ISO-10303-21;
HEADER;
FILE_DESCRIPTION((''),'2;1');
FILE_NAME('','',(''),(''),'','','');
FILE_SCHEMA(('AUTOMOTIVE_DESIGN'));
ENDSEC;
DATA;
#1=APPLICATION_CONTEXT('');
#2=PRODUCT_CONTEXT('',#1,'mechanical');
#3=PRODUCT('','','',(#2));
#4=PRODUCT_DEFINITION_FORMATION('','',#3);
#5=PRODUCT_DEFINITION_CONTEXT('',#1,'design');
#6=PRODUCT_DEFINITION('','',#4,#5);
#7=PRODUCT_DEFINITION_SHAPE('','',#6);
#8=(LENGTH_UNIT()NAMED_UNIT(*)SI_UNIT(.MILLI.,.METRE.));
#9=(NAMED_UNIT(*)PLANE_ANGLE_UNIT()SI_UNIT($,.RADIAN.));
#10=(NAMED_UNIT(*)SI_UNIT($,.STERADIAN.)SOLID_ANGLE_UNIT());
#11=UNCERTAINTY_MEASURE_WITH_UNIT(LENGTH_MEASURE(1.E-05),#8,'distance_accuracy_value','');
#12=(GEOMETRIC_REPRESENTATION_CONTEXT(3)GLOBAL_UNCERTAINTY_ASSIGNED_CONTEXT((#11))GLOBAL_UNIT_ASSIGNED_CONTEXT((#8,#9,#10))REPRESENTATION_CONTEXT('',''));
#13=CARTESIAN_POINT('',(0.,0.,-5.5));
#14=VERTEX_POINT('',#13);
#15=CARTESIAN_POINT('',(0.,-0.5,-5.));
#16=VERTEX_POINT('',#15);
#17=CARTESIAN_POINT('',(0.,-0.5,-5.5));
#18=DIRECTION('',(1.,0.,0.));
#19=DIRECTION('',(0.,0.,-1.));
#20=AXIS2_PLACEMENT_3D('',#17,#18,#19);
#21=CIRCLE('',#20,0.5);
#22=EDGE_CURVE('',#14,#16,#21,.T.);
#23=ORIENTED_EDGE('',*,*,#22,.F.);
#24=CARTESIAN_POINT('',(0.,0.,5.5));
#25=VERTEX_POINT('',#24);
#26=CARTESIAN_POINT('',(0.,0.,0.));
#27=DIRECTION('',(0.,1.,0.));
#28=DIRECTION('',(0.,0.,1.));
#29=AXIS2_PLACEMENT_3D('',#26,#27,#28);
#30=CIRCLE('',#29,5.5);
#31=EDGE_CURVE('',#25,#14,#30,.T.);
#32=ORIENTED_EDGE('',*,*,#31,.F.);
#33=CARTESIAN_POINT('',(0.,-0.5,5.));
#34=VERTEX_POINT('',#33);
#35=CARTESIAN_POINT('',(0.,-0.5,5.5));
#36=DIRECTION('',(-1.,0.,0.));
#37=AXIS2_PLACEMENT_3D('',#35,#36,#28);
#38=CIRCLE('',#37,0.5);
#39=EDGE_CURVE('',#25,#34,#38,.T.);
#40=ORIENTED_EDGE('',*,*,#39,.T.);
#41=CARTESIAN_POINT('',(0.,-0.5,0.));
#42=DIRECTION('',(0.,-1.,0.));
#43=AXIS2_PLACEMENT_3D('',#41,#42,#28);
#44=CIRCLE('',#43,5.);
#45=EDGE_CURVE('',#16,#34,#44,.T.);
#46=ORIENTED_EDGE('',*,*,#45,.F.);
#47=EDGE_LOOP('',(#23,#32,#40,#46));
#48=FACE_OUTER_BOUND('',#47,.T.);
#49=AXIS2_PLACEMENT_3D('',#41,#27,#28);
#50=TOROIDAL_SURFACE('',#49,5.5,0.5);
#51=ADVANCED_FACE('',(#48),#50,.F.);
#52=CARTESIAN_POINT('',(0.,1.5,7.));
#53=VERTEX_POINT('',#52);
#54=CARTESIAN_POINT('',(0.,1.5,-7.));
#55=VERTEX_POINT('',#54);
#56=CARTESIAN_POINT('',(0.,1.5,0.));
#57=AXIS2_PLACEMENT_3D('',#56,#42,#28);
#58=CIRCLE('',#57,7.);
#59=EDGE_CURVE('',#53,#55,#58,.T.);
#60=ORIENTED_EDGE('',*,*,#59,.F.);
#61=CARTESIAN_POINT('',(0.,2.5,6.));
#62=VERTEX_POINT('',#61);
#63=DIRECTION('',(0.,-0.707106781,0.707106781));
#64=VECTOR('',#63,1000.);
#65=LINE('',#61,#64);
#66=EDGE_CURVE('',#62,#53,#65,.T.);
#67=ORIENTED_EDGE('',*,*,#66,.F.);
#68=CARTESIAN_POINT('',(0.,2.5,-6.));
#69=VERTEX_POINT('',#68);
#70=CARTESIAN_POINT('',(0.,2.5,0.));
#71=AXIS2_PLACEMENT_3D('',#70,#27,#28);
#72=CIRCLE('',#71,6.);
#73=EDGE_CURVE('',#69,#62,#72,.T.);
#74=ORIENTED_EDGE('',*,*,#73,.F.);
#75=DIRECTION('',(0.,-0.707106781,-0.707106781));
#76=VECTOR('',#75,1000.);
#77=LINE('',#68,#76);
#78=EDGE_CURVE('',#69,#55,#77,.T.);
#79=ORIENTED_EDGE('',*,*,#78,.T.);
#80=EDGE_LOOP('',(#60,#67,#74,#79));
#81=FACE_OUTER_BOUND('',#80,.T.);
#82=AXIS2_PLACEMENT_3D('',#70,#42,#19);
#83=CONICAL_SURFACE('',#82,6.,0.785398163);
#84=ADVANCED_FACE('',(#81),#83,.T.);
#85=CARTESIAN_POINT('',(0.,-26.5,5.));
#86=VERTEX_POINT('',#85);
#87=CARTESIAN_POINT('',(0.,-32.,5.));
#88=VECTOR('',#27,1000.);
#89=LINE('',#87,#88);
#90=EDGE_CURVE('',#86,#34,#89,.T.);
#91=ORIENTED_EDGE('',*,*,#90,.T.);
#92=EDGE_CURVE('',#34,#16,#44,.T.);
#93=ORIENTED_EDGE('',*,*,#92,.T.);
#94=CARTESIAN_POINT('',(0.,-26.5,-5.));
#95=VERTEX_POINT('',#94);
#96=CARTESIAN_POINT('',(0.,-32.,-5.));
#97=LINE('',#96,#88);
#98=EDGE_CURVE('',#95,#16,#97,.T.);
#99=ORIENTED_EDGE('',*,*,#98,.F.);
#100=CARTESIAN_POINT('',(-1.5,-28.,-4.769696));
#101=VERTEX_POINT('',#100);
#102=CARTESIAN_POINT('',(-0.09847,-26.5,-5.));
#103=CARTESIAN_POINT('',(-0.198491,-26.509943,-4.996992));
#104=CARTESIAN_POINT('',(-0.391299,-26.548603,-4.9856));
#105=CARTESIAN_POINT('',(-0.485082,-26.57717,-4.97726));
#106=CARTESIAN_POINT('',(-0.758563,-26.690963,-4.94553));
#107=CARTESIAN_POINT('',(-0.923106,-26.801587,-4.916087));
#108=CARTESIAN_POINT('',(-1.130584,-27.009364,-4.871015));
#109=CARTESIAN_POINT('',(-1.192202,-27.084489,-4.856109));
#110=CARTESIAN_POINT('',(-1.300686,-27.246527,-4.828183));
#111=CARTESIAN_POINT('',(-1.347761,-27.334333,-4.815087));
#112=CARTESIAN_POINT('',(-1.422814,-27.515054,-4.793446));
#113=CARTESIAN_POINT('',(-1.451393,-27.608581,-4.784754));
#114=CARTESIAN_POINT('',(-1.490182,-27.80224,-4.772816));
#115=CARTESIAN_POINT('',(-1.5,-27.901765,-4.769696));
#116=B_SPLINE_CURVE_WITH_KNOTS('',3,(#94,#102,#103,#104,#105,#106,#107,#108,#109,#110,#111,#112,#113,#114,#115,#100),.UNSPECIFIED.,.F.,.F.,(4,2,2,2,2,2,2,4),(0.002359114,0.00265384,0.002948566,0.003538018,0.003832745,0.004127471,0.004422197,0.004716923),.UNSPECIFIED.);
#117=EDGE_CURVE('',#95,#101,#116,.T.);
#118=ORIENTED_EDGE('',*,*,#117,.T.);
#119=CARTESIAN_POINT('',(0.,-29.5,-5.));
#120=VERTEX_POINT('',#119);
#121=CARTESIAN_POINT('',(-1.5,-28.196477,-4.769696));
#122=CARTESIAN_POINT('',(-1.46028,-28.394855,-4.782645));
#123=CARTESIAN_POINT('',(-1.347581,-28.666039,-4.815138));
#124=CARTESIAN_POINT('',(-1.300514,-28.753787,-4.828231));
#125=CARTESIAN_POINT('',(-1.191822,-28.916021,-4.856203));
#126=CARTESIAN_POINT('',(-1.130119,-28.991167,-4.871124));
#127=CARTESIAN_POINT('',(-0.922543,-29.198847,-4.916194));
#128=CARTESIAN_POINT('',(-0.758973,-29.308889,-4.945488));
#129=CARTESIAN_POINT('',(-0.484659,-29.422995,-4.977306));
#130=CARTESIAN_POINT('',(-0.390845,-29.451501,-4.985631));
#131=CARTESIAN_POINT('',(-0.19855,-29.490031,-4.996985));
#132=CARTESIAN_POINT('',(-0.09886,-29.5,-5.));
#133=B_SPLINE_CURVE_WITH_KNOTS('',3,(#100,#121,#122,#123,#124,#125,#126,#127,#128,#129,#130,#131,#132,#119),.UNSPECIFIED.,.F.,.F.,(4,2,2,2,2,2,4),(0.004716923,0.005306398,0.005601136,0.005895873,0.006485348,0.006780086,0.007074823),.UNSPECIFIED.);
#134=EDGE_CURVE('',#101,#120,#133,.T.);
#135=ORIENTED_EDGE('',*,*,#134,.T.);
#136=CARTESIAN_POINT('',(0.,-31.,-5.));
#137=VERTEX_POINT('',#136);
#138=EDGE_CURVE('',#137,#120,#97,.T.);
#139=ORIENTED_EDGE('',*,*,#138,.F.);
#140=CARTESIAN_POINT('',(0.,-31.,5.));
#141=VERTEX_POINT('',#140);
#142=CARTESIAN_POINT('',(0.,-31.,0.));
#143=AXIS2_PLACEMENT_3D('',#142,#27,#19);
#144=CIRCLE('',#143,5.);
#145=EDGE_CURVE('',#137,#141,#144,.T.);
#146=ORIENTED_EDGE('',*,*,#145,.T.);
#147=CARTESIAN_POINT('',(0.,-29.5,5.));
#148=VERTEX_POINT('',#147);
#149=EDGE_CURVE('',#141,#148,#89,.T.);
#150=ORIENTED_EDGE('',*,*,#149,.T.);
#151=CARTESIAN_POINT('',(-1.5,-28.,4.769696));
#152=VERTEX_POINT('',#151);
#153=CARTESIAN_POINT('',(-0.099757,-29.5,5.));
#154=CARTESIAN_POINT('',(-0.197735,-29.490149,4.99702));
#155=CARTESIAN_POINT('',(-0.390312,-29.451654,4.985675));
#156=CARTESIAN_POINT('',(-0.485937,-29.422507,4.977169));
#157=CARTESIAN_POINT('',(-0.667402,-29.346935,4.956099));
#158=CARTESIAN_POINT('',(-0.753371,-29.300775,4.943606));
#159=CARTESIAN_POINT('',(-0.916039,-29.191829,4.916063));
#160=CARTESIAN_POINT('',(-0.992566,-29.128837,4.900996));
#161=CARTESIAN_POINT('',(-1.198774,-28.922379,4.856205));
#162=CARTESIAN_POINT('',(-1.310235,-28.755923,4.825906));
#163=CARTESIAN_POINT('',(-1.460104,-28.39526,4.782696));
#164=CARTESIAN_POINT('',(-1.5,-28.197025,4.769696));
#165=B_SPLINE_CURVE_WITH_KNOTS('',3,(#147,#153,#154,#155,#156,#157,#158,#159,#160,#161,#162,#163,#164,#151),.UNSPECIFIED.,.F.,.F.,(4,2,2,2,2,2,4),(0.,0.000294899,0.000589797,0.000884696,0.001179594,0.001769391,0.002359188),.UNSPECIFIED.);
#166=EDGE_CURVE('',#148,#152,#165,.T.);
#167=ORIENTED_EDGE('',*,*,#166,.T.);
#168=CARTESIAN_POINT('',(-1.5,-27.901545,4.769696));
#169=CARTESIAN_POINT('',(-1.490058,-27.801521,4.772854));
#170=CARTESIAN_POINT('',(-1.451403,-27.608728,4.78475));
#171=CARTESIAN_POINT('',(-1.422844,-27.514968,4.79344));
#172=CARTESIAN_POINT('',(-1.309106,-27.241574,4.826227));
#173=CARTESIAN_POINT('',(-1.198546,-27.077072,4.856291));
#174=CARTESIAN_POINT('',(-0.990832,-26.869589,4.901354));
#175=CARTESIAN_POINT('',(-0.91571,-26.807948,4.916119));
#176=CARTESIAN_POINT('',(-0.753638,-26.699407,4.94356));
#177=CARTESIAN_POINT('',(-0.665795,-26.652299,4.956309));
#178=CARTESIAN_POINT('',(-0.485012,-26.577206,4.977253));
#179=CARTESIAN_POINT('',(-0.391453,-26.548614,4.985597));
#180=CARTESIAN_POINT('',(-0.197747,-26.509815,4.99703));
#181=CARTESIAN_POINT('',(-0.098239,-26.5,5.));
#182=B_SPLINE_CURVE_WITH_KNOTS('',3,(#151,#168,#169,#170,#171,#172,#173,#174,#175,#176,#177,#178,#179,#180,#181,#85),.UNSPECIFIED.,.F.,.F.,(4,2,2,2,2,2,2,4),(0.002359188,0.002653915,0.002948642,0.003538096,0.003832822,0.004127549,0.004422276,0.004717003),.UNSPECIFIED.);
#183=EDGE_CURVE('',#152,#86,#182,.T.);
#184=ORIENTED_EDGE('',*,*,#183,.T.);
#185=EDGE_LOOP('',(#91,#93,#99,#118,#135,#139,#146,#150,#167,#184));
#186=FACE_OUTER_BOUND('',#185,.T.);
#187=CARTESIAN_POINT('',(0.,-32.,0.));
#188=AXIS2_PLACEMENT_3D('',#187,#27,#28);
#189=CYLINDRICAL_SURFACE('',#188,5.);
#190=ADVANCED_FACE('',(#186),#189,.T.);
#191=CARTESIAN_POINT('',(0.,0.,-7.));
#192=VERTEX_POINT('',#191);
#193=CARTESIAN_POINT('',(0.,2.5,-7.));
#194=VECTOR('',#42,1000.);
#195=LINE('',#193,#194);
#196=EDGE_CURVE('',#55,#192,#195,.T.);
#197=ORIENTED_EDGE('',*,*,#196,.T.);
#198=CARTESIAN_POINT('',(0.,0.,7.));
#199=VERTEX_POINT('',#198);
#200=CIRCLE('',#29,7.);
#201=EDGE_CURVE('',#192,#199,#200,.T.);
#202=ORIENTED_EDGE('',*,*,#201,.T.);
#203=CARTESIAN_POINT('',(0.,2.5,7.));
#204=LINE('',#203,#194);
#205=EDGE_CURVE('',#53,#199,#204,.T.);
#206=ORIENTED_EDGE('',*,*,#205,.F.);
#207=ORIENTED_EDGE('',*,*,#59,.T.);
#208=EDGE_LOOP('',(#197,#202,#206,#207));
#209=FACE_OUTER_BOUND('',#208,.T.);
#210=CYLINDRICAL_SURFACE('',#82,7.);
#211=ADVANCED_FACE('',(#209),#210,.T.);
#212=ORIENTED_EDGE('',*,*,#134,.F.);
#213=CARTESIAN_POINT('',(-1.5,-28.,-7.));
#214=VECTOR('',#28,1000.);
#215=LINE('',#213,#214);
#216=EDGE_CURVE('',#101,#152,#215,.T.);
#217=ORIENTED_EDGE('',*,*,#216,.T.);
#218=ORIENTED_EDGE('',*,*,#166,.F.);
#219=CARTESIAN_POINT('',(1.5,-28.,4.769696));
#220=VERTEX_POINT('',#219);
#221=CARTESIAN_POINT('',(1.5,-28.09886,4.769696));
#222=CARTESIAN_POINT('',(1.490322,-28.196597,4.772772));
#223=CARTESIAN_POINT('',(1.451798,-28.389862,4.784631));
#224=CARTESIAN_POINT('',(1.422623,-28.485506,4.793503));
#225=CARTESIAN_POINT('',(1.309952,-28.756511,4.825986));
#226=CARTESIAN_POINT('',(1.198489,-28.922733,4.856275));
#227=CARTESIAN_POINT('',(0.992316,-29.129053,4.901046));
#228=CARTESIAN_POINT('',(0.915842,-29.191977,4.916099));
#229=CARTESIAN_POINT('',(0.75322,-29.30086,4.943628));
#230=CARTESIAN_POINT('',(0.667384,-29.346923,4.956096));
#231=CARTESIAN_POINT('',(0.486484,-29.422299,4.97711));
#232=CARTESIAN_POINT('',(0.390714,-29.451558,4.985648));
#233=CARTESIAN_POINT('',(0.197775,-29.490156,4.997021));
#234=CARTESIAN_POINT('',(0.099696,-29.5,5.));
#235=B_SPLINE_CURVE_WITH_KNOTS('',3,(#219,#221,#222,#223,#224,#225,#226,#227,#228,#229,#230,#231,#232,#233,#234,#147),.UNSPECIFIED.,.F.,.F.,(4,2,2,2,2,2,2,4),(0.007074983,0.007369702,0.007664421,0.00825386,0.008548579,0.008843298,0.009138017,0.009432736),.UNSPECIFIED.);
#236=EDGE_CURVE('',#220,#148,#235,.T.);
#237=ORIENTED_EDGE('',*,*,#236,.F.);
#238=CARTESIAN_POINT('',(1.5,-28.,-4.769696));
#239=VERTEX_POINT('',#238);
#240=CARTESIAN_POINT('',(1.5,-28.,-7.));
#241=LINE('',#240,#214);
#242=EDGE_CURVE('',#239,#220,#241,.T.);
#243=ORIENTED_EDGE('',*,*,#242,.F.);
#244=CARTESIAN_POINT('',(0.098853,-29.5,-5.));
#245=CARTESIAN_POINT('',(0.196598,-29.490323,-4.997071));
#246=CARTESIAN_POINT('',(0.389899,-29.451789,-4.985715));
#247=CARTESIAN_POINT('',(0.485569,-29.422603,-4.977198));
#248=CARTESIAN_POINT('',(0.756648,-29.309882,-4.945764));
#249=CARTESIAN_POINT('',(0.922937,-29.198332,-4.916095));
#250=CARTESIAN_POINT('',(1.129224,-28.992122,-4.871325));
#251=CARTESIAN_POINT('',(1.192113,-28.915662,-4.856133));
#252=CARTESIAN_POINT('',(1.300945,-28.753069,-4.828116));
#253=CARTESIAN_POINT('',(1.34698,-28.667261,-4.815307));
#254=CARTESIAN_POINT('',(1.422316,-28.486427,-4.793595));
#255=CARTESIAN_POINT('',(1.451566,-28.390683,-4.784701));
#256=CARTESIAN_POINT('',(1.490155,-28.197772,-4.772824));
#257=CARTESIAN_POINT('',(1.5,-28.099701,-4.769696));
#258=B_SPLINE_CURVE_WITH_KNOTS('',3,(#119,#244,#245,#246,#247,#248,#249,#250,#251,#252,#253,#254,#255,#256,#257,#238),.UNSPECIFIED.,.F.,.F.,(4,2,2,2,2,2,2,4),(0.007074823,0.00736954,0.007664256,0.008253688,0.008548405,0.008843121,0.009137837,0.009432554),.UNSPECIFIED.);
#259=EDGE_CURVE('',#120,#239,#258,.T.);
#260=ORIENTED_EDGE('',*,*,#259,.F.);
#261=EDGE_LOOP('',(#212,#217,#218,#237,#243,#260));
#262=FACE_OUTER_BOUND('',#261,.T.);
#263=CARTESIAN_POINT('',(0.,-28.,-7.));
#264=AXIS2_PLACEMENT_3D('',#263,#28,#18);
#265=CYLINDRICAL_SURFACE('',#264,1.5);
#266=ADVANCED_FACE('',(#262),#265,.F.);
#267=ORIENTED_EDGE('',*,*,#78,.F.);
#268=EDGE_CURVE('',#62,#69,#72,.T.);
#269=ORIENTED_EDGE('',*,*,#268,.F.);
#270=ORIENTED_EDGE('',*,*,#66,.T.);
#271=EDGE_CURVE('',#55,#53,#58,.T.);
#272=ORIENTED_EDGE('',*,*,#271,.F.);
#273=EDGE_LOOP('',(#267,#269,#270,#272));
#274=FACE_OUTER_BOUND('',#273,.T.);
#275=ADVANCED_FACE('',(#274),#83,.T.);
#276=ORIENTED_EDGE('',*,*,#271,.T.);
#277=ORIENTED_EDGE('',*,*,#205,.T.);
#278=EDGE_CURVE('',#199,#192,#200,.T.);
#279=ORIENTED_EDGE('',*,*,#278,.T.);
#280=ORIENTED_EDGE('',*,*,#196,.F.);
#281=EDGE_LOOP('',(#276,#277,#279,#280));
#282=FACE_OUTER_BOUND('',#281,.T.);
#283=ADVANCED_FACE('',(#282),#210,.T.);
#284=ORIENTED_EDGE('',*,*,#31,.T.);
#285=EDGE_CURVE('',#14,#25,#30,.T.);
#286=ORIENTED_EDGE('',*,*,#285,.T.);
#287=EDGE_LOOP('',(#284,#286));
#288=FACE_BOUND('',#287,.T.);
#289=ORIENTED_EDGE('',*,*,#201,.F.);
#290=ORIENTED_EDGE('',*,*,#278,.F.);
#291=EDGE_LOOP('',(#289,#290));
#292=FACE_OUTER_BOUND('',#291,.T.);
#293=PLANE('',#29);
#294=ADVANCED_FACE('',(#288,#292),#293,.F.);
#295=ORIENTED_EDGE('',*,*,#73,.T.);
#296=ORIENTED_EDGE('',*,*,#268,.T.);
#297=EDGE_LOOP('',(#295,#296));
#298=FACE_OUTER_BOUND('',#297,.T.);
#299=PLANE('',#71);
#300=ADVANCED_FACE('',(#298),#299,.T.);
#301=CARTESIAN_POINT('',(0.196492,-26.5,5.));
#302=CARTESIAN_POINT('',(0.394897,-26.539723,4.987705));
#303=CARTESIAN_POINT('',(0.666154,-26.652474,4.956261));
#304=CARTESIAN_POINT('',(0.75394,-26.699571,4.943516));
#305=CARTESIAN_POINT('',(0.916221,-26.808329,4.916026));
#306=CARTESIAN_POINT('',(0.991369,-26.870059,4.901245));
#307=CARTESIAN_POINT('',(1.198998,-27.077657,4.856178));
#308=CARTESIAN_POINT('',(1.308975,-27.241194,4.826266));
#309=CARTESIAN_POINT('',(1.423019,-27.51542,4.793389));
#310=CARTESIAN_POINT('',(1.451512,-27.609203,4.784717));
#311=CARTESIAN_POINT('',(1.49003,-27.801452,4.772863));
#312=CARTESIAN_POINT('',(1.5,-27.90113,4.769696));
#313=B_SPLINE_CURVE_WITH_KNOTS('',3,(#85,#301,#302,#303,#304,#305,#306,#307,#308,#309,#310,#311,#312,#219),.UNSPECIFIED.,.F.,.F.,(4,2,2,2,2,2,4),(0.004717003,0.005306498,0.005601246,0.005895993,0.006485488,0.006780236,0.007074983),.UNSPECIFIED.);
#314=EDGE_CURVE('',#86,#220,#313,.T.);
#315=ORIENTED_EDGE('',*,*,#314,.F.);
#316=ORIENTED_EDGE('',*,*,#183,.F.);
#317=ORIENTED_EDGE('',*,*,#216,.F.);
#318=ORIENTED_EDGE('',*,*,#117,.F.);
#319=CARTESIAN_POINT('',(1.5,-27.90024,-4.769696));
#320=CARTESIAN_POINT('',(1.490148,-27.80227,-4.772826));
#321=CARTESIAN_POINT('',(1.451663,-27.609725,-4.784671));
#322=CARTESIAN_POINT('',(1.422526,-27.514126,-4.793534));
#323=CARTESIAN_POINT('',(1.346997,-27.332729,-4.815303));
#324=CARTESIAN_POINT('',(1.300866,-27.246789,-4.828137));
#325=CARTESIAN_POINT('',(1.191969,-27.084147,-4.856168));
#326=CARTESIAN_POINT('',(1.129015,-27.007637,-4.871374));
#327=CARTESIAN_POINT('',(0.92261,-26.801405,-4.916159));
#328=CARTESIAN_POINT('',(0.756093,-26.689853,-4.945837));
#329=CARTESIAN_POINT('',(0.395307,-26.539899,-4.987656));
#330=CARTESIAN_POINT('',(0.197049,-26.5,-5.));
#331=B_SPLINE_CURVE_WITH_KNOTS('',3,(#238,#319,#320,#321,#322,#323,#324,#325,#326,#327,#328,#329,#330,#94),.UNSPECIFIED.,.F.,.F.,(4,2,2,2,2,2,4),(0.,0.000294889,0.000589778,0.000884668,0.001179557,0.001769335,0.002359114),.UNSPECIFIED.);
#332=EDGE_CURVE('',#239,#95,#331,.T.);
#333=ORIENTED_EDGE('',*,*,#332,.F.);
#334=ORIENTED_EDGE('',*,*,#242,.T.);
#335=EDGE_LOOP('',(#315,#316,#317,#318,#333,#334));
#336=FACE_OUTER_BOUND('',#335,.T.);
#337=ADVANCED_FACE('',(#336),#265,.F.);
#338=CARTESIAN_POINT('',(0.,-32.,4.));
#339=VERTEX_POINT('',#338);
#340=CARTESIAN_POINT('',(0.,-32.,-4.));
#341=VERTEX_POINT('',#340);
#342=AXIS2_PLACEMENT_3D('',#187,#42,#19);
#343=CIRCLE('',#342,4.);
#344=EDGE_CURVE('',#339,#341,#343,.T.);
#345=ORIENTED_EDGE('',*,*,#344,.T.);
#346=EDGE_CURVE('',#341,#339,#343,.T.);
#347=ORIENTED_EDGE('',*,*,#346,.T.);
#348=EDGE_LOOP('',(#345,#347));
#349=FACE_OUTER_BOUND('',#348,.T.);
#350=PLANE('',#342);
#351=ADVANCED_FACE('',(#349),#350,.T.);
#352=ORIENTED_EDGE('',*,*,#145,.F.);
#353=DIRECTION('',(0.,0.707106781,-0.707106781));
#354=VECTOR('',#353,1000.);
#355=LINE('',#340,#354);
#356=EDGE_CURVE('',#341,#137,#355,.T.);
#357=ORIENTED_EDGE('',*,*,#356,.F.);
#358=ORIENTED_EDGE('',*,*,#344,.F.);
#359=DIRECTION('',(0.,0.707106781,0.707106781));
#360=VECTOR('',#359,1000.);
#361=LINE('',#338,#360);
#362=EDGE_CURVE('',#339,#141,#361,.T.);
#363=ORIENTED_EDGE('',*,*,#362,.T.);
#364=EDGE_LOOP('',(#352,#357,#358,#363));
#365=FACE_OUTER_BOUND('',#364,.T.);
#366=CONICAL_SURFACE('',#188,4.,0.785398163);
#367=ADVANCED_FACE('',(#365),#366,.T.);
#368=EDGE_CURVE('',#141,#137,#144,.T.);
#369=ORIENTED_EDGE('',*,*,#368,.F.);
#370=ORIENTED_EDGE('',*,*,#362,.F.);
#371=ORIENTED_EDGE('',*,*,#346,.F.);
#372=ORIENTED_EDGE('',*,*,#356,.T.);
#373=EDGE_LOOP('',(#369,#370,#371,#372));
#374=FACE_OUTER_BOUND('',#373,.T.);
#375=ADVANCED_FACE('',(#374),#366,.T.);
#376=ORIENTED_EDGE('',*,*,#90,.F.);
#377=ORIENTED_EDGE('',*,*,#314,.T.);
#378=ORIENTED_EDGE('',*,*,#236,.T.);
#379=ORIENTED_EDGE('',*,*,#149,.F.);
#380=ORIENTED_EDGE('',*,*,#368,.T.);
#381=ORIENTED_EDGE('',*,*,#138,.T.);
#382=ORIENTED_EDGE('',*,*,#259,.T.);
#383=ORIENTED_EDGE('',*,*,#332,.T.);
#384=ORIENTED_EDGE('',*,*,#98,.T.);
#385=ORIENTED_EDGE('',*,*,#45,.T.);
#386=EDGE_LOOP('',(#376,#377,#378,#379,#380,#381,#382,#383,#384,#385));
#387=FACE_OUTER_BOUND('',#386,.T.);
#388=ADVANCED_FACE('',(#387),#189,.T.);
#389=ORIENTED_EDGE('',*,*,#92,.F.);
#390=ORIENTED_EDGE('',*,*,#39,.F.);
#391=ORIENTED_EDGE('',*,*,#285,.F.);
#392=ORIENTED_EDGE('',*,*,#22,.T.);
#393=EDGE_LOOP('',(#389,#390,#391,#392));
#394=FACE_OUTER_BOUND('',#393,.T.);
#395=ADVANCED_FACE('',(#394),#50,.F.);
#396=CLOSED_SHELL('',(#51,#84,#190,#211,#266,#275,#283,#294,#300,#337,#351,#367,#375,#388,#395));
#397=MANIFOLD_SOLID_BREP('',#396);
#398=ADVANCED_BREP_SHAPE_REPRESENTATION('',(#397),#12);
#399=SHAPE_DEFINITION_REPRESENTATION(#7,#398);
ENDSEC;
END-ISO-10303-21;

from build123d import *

# Parameters (mm, degrees)
SKETCH_1_R               = 7
EXTRUDE_1_DEPTH          = 2.5
SKETCH_2_R               = 5
EXTRUDE_2_DEPTH          = 32
CHAMFER_1_SIZE           = 1
CUT_EXTRUDE_2_DEPTH      = 34.496268449
CUT_EXTRUDE_2_DEPTH_BACK = 34.496268449
SKETCH_10_R              = 1.5
FILLET_1_R               = 0.5


with BuildPart() as part:
    # 草图1 → 凸台-拉伸1 (new body)
    with BuildSketch(Plane(origin=(0, 0, 0), x_dir=(1, 0, 0), z_dir=(0, 1, 0))):
        with Locations(Location((0, 0, 0), (0, 0, 270))):
            Circle(SKETCH_1_R)
    extrude(amount=EXTRUDE_1_DEPTH)

    # 草图2 → 凸台-拉伸2 (add)
    with BuildSketch(Plane.XZ):
        with Locations(Location((0, 0, 0), (0, 0, 270))):
            Circle(SKETCH_2_R)
    extrude(amount=EXTRUDE_2_DEPTH)

    # 倒角1
    chamfer_1_edges = [part.edges().sort_by_distance(p)[0] for p in [
        (0, 2.5, -7),
        (0, -32, 5),
    ]]
    chamfer(chamfer_1_edges, length=CHAMFER_1_SIZE)

    # 草图10 → 切除-拉伸2 (cut, two sides: drawn at the far end of the back side and taken through both)
    with BuildSketch(Plane.XY.offset(-CUT_EXTRUDE_2_DEPTH_BACK)):
        with Locations(Location((0, -28, 0), (0, 0, 270.000000018))):
            Circle(SKETCH_10_R)
    extrude(amount=CUT_EXTRUDE_2_DEPTH + CUT_EXTRUDE_2_DEPTH_BACK, mode=Mode.SUBTRACT)

    # 圆角1
    fillet_1_edges = [part.edges().sort_by_distance(p)[0] for p in [
        (0, 0, 5),
    ]]
    fillet(fillet_1_edges, radius=FILLET_1_R)


solid = part.part
